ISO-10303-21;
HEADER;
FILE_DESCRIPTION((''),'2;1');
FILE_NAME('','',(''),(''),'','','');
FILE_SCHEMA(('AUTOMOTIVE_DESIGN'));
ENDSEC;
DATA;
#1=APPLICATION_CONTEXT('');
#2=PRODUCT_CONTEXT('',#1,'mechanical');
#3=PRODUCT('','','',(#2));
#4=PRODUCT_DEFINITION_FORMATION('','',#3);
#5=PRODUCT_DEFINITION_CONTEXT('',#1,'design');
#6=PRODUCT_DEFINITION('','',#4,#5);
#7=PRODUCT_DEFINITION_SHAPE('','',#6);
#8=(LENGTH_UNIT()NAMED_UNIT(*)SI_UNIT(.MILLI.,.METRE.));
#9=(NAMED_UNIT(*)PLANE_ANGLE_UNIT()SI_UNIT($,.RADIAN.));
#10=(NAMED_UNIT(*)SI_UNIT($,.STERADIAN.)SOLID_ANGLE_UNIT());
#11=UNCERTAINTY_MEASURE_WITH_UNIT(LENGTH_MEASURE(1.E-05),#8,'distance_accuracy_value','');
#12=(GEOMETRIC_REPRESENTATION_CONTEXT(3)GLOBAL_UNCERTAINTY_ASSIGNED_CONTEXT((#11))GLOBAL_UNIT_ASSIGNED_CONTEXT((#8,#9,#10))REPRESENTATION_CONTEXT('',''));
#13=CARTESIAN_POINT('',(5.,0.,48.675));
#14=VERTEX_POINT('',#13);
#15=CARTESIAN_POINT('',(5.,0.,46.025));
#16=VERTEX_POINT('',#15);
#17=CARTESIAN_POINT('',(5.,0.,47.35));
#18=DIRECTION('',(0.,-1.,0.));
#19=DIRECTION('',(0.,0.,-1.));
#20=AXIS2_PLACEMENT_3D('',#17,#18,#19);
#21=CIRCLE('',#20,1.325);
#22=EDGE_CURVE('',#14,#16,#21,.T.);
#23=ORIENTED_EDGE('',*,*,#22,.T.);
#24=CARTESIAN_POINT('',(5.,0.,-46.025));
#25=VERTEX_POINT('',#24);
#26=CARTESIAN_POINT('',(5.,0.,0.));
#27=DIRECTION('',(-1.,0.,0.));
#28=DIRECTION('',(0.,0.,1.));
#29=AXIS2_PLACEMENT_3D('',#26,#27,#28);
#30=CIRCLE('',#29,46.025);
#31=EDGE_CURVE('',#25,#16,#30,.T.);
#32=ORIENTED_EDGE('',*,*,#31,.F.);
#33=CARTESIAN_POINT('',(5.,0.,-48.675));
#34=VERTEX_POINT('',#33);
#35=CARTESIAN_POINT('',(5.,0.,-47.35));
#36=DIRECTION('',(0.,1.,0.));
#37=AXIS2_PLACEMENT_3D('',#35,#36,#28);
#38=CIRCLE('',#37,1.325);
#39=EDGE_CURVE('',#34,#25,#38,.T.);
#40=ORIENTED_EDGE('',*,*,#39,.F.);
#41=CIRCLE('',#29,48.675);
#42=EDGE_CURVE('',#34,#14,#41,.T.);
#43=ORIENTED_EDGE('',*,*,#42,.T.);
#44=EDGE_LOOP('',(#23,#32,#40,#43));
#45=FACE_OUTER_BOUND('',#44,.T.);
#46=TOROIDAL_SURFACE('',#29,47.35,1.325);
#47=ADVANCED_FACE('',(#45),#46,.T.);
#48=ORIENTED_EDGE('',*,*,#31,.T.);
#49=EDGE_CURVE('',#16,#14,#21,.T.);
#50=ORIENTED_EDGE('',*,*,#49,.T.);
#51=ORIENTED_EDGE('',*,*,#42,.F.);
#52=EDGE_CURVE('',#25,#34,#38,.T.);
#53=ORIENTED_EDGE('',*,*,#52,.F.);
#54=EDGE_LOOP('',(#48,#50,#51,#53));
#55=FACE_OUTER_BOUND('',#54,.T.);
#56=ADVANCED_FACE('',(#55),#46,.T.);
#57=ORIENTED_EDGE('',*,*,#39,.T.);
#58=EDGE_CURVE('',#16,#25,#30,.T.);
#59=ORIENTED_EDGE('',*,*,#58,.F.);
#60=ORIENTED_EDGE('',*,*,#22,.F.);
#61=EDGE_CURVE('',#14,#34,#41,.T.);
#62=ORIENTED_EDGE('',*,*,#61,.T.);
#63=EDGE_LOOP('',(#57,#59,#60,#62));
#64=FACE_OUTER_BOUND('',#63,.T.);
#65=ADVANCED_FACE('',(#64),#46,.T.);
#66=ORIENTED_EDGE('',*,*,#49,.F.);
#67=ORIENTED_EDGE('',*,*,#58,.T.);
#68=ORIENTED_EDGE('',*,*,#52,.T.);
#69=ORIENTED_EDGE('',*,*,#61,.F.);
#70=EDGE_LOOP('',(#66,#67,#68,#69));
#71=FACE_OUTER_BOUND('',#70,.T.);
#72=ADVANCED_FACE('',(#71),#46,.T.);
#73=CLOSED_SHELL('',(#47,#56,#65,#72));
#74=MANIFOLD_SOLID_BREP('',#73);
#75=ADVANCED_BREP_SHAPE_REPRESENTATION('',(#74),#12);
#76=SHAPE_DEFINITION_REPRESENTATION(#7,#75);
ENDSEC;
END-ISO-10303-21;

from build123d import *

# Parameters (mm, degrees)
SKETCH1_R = 1.325


with BuildPart() as part:
    # Sketch1 → Revolve1 (revolve)
    with BuildSketch(Plane.XY, mode=Mode.PRIVATE) as revolve1_sk:
        with Locations((5, 47.35)):
            Circle(SKETCH1_R)
    revolve(revolve1_sk.sketch.rotate(Axis((0, 0, 0), (1, 0, 0)), 90), axis=Axis((0, 0, 0), (1, 0, 0)))


solid = part.part
